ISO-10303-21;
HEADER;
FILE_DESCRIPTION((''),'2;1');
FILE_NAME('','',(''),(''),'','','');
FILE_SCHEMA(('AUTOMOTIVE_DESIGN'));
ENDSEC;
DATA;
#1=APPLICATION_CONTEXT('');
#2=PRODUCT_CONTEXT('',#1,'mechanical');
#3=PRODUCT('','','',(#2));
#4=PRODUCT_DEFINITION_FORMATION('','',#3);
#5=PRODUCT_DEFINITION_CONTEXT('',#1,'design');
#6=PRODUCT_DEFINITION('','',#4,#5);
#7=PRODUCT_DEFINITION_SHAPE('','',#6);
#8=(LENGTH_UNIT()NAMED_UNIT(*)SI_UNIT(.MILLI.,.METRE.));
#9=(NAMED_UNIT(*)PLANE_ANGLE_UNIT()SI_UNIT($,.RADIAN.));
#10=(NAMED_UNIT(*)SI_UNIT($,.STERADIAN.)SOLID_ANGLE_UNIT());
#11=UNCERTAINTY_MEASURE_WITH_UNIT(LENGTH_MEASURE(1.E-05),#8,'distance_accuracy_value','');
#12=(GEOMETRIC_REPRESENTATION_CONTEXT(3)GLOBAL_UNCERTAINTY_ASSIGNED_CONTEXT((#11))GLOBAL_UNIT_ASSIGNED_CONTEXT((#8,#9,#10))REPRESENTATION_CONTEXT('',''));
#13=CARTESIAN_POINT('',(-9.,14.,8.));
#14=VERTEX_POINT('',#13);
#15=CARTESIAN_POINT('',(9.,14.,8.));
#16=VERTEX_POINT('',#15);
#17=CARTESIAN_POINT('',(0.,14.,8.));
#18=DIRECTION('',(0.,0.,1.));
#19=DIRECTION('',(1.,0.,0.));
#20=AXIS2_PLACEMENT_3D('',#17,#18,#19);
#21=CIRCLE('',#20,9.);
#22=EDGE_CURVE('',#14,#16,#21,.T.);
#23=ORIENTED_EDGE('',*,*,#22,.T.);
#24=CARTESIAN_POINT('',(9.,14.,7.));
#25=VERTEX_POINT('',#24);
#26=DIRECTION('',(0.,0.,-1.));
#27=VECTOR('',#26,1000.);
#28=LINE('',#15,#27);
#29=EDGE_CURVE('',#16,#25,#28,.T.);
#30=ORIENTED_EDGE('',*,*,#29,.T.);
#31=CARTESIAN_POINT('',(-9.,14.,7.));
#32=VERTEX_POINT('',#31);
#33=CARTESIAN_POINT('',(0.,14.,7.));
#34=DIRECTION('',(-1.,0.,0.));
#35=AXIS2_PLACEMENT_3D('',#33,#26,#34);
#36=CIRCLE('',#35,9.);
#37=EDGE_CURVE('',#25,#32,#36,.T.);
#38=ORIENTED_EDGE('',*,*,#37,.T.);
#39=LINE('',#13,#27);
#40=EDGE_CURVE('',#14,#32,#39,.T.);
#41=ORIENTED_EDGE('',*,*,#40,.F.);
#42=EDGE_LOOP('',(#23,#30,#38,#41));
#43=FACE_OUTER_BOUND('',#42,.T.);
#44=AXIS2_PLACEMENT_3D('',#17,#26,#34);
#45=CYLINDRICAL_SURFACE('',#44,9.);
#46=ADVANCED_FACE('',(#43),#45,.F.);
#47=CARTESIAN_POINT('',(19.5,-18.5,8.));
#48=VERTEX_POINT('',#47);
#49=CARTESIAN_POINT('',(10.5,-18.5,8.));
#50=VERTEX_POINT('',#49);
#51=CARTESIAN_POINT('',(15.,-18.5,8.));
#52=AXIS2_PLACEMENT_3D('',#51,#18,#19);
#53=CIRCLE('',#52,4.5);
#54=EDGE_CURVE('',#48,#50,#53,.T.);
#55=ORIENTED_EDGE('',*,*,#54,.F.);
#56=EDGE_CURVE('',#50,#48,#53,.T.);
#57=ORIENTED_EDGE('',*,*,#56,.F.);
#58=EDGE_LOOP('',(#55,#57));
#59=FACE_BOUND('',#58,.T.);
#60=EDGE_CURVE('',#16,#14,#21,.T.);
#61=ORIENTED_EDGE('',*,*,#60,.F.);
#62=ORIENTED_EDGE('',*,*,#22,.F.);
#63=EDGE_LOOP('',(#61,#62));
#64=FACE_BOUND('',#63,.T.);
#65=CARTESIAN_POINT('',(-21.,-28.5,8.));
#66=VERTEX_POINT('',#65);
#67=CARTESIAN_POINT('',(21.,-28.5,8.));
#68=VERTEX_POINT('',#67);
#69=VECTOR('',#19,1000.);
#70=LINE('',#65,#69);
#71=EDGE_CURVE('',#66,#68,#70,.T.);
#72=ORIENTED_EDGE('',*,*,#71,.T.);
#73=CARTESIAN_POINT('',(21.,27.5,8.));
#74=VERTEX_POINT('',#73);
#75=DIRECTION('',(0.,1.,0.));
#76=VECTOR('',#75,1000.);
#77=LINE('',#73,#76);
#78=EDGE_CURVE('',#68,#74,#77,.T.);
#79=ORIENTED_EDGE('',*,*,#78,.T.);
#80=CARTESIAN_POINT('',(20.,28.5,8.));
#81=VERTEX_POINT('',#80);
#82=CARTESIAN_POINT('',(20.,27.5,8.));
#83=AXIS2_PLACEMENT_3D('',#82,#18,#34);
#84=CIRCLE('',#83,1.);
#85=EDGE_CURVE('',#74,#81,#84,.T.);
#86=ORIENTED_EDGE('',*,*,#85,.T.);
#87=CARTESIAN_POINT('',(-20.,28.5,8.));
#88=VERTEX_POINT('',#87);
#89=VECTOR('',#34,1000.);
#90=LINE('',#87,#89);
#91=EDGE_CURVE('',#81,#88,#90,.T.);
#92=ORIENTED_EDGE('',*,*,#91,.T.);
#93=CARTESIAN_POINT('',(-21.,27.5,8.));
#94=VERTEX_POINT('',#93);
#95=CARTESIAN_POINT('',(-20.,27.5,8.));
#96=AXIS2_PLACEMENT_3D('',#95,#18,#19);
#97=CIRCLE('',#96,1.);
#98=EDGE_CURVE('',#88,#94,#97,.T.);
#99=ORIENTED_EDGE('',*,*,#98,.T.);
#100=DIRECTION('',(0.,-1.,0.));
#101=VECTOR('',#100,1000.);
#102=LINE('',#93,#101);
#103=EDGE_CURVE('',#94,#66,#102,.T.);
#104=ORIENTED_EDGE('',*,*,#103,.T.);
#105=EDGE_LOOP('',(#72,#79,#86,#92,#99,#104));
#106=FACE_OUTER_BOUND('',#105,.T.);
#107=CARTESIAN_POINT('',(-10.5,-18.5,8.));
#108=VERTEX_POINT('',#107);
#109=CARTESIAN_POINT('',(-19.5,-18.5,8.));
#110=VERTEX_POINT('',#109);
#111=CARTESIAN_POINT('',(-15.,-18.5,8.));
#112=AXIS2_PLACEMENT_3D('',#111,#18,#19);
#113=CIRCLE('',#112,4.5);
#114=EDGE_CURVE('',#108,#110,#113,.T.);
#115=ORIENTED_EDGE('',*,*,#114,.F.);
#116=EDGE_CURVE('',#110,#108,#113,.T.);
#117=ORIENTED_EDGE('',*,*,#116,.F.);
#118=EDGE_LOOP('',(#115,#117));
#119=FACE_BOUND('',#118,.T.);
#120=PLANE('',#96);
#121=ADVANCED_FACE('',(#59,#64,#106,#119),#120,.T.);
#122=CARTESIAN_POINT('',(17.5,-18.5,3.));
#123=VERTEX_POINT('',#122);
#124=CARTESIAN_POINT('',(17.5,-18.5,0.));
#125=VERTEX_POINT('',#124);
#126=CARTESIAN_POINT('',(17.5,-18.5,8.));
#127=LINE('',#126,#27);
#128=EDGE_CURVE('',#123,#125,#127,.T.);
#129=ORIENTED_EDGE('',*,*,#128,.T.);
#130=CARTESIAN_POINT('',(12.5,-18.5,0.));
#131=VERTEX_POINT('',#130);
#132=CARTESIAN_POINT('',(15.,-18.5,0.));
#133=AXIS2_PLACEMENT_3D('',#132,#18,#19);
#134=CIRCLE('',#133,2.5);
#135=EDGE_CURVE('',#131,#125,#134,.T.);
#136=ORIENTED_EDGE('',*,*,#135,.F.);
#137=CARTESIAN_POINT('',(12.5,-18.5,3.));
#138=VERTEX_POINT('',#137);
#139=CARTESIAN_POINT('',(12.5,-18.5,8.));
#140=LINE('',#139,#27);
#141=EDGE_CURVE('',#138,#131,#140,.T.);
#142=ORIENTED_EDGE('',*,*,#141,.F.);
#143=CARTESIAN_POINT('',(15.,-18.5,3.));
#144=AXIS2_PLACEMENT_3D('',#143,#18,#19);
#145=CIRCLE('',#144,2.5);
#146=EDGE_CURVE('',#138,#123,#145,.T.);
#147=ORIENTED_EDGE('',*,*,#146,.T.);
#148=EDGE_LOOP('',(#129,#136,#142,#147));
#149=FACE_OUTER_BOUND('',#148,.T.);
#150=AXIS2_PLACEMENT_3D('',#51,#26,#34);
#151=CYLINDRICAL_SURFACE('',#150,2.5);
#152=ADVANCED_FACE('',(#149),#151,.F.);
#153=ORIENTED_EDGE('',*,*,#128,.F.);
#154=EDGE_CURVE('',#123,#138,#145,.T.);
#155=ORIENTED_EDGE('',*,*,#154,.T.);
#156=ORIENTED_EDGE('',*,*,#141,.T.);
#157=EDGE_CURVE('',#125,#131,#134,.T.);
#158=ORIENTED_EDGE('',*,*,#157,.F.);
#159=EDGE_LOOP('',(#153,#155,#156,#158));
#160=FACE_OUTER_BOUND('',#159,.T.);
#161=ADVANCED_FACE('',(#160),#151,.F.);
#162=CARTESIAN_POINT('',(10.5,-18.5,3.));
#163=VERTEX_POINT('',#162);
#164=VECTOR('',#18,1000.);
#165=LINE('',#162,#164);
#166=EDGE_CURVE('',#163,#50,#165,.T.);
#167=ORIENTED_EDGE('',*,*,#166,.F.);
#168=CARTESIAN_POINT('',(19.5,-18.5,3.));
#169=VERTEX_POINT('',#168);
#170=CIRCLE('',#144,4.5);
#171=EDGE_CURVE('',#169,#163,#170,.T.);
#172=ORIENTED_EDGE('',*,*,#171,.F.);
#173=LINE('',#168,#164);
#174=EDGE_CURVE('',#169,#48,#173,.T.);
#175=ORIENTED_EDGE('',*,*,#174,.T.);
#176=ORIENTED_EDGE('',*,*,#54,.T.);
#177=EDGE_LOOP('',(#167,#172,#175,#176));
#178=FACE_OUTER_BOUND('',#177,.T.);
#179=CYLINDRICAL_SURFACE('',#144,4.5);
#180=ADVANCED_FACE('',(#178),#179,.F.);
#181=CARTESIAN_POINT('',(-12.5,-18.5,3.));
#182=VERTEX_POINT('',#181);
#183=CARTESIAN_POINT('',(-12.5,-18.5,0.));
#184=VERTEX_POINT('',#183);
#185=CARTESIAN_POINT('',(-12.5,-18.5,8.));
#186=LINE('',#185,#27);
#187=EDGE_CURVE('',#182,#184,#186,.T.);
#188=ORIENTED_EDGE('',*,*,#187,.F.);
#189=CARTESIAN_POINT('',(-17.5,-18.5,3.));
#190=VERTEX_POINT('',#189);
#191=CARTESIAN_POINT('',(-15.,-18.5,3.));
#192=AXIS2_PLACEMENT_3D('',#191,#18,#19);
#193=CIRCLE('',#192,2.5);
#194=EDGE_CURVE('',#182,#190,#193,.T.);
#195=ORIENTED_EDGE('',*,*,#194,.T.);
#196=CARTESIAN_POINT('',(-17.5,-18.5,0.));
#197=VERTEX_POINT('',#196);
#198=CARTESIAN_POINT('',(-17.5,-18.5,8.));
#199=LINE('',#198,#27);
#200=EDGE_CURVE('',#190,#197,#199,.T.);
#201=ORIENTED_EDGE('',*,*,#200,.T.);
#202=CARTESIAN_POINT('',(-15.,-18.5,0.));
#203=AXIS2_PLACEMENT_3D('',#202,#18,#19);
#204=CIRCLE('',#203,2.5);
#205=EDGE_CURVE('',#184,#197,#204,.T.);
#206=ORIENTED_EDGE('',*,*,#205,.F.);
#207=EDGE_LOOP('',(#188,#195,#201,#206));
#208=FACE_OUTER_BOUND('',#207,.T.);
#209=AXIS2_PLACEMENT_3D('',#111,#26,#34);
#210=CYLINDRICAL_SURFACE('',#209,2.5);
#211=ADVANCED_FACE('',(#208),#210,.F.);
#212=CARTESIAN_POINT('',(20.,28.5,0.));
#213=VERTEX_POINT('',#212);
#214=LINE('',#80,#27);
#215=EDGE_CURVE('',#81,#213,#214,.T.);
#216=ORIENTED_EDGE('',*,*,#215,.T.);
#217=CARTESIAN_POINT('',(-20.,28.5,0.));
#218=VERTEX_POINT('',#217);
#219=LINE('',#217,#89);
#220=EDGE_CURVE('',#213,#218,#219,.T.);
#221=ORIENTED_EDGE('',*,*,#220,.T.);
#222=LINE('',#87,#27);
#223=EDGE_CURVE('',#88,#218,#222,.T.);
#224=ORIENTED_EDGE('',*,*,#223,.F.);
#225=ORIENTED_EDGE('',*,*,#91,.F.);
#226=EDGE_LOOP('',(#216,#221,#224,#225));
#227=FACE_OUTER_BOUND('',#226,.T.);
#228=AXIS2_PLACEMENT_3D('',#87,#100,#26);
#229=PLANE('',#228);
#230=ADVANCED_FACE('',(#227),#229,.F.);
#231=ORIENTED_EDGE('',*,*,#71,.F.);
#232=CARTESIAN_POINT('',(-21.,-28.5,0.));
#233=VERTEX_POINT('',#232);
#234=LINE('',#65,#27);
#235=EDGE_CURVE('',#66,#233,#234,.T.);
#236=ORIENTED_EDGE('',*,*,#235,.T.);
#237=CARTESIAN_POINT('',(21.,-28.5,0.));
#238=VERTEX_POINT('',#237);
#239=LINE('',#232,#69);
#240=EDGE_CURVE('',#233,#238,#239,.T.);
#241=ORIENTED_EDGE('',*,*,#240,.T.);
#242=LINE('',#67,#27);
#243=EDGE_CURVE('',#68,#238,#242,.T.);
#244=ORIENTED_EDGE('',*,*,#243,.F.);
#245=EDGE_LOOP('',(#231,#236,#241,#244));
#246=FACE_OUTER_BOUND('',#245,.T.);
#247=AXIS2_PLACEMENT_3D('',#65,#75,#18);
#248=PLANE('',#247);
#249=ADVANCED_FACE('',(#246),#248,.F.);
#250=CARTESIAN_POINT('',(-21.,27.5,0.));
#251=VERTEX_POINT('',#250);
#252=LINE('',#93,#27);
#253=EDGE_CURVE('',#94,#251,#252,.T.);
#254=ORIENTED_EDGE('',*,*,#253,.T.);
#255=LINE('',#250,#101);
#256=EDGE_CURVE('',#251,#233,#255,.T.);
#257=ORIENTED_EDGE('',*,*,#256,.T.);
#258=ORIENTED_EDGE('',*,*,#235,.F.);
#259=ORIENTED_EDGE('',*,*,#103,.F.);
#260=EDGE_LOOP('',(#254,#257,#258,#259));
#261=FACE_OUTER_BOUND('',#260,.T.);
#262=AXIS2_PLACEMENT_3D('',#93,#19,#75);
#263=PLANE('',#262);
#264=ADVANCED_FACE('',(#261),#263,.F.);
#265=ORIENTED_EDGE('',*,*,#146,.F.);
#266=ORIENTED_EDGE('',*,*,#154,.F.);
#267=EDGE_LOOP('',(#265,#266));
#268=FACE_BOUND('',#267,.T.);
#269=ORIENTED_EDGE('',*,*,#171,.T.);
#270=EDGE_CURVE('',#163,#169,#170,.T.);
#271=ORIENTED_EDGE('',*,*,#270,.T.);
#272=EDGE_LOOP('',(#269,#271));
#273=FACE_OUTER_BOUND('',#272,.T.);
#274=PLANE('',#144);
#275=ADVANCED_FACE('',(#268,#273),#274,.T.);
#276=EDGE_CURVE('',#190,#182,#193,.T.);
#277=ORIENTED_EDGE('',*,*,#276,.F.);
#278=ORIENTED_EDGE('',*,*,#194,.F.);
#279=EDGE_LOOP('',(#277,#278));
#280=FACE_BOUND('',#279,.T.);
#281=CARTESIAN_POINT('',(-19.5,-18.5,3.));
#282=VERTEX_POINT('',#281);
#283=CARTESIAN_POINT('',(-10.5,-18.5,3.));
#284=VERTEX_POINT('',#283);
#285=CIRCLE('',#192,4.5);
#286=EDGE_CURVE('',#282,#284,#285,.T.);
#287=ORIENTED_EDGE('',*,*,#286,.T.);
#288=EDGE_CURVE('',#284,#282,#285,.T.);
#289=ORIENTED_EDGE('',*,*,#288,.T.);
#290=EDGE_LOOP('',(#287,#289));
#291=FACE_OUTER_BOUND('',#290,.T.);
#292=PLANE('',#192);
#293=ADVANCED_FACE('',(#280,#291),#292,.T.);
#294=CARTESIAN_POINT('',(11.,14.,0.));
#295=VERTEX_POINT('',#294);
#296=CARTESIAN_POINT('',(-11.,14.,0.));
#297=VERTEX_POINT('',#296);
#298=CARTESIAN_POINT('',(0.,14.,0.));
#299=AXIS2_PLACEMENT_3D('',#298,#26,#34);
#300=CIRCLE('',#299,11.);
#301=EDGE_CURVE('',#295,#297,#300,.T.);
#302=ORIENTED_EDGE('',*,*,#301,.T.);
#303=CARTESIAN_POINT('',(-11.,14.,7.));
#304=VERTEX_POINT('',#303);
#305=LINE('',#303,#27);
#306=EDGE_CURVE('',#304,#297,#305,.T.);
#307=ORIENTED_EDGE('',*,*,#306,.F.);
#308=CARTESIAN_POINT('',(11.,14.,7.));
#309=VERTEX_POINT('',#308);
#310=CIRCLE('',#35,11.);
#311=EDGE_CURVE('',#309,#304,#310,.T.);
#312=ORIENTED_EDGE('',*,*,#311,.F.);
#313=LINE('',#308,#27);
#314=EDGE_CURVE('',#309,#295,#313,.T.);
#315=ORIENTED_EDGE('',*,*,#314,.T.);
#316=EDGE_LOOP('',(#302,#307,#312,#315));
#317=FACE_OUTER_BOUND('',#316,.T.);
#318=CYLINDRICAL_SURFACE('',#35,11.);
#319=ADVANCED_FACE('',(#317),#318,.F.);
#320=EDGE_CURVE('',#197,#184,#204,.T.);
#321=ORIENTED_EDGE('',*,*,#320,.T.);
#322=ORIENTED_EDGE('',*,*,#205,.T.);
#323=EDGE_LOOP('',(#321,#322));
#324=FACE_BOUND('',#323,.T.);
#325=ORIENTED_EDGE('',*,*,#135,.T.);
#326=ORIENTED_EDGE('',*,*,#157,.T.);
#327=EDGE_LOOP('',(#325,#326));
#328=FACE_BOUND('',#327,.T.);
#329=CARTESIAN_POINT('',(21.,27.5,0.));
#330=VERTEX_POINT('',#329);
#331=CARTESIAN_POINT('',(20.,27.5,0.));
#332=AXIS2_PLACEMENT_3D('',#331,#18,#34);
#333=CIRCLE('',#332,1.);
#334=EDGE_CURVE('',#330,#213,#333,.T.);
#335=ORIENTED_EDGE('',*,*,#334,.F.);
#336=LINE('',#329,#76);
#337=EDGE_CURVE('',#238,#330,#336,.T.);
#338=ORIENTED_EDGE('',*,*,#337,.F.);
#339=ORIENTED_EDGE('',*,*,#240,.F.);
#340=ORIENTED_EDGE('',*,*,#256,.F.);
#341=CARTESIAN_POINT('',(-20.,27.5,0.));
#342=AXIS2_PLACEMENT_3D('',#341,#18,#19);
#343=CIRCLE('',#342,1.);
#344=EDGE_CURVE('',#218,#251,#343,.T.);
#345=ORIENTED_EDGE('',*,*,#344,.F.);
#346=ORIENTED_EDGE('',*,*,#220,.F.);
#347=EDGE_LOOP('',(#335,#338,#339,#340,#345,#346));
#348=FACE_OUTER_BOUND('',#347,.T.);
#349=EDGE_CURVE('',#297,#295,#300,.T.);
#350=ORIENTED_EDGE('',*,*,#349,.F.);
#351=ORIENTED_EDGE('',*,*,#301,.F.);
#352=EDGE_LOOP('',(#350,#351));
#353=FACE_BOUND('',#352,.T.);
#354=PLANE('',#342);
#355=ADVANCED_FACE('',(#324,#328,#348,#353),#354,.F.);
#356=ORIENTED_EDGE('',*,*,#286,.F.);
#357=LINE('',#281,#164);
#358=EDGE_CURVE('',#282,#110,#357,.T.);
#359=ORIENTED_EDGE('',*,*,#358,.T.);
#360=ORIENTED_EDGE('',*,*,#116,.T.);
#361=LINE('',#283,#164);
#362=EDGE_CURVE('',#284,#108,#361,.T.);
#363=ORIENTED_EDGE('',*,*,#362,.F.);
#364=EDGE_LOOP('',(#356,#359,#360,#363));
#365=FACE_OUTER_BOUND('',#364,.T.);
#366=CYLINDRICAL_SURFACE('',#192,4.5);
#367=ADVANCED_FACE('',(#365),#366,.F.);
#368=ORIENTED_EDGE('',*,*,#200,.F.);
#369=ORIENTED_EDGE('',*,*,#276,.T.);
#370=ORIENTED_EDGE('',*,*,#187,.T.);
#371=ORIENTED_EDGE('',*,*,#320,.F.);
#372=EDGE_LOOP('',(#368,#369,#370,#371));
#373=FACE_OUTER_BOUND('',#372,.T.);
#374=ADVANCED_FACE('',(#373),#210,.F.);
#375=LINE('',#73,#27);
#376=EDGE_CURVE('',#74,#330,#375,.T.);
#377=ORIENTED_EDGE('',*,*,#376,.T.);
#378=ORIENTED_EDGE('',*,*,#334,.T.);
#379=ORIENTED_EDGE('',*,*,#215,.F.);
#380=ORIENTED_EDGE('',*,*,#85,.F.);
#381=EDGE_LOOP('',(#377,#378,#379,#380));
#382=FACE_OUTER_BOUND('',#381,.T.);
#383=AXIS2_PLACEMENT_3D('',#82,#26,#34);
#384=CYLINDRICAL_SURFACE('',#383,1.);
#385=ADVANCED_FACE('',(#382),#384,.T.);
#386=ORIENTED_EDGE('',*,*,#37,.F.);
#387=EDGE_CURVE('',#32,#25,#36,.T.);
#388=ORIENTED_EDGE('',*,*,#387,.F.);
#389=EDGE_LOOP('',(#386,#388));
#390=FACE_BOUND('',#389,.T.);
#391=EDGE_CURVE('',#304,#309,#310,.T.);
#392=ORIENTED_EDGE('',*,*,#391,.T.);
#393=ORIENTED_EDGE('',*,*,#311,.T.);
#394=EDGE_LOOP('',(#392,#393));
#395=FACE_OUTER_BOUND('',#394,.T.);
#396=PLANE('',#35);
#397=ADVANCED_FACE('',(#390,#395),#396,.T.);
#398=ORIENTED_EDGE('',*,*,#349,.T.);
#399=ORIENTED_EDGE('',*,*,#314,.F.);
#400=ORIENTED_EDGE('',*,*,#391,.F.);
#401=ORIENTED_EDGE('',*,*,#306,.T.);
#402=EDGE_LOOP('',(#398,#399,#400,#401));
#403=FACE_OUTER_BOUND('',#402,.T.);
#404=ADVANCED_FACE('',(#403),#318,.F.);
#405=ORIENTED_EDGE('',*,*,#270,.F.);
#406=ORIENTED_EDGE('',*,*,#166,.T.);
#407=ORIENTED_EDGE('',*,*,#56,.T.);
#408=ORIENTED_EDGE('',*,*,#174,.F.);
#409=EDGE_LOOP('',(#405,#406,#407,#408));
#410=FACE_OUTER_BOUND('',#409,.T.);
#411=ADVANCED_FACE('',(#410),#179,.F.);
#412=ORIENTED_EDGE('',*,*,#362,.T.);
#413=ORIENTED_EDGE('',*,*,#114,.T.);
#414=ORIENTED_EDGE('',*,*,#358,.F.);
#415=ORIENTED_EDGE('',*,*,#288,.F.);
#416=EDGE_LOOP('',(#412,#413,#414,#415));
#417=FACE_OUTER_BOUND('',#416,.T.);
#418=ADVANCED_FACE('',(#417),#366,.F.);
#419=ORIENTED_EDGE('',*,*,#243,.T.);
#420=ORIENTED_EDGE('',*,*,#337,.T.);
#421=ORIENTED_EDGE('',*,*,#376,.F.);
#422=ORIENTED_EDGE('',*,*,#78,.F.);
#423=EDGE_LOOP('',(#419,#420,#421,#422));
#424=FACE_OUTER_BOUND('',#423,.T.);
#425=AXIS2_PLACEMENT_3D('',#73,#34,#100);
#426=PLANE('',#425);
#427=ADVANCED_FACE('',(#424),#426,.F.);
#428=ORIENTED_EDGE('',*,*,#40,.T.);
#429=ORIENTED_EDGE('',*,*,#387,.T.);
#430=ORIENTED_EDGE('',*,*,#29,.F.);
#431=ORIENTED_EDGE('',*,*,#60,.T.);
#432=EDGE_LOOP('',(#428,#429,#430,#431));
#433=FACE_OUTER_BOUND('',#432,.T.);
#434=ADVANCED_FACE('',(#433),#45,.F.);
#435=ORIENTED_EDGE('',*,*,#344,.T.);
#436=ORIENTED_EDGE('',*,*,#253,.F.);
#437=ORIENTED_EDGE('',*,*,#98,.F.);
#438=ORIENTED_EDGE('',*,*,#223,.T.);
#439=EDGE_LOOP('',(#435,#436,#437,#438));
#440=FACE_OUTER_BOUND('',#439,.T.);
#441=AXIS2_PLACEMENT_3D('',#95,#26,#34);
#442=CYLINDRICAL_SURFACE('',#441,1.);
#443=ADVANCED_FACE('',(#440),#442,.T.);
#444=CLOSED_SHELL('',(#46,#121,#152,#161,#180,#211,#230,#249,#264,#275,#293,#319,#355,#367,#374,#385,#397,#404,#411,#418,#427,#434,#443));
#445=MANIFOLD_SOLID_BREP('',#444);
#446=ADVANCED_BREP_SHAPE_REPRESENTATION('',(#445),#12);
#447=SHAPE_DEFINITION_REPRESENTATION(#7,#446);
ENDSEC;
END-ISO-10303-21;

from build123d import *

# Parameters (mm, degrees)
SKETCH1_R           = 9
SKETCH1_R_2         = 2.5
BOSS_EXTRUDE1_DEPTH = 8
SKETCH2_R           = 4.5
CUT_EXTRUDE1_DEPTH  = 5
SKETCH3_R           = 11
CUT_EXTRUDE2_DEPTH  = 7


with BuildPart() as part:
    # Sketch1 → Boss-Extrude1 (new body)
    with BuildSketch(Plane.XY):
        with BuildLine():
            Line((-20, 28.5), (20, 28.5))
            ThreePointArc((20, 28.5), (20.707106781, 28.207106781), (21, 27.5))
            Line((21, 27.5), (21, -28.5))
            Line((21, -28.5), (-21, -28.5))
            Line((-21, -28.5), (-21, 27.5))
            ThreePointArc((-21, 27.5), (-20.707106781, 28.207106781), (-20, 28.5))
        make_face()
        with Locations((0, 14)):
            Circle(SKETCH1_R, mode=Mode.SUBTRACT)
        with Locations((-15, -18.5)):
            Circle(SKETCH1_R_2, mode=Mode.SUBTRACT)
        with Locations((15, -18.5)):
            Circle(SKETCH1_R_2, mode=Mode.SUBTRACT)
    extrude(amount=BOSS_EXTRUDE1_DEPTH)

    # Sketch2 → Cut-Extrude1 (cut)
    with BuildSketch(Plane.XY.offset(8)):
        with Locations((-15, -18.5)):
            Circle(SKETCH2_R)
        with Locations((15, -18.5)):
            Circle(SKETCH2_R)
    extrude(amount=-CUT_EXTRUDE1_DEPTH, mode=Mode.SUBTRACT)

    # Sketch3 → Cut-Extrude2 (cut)
    with BuildSketch(Plane(origin=(0, 0, 0), x_dir=(-1, 0, 0), z_dir=(0, 0, -1))):
        with Locations((0, 14)):
            Circle(SKETCH3_R)
    extrude(amount=-CUT_EXTRUDE2_DEPTH, mode=Mode.SUBTRACT)


solid = part.part
